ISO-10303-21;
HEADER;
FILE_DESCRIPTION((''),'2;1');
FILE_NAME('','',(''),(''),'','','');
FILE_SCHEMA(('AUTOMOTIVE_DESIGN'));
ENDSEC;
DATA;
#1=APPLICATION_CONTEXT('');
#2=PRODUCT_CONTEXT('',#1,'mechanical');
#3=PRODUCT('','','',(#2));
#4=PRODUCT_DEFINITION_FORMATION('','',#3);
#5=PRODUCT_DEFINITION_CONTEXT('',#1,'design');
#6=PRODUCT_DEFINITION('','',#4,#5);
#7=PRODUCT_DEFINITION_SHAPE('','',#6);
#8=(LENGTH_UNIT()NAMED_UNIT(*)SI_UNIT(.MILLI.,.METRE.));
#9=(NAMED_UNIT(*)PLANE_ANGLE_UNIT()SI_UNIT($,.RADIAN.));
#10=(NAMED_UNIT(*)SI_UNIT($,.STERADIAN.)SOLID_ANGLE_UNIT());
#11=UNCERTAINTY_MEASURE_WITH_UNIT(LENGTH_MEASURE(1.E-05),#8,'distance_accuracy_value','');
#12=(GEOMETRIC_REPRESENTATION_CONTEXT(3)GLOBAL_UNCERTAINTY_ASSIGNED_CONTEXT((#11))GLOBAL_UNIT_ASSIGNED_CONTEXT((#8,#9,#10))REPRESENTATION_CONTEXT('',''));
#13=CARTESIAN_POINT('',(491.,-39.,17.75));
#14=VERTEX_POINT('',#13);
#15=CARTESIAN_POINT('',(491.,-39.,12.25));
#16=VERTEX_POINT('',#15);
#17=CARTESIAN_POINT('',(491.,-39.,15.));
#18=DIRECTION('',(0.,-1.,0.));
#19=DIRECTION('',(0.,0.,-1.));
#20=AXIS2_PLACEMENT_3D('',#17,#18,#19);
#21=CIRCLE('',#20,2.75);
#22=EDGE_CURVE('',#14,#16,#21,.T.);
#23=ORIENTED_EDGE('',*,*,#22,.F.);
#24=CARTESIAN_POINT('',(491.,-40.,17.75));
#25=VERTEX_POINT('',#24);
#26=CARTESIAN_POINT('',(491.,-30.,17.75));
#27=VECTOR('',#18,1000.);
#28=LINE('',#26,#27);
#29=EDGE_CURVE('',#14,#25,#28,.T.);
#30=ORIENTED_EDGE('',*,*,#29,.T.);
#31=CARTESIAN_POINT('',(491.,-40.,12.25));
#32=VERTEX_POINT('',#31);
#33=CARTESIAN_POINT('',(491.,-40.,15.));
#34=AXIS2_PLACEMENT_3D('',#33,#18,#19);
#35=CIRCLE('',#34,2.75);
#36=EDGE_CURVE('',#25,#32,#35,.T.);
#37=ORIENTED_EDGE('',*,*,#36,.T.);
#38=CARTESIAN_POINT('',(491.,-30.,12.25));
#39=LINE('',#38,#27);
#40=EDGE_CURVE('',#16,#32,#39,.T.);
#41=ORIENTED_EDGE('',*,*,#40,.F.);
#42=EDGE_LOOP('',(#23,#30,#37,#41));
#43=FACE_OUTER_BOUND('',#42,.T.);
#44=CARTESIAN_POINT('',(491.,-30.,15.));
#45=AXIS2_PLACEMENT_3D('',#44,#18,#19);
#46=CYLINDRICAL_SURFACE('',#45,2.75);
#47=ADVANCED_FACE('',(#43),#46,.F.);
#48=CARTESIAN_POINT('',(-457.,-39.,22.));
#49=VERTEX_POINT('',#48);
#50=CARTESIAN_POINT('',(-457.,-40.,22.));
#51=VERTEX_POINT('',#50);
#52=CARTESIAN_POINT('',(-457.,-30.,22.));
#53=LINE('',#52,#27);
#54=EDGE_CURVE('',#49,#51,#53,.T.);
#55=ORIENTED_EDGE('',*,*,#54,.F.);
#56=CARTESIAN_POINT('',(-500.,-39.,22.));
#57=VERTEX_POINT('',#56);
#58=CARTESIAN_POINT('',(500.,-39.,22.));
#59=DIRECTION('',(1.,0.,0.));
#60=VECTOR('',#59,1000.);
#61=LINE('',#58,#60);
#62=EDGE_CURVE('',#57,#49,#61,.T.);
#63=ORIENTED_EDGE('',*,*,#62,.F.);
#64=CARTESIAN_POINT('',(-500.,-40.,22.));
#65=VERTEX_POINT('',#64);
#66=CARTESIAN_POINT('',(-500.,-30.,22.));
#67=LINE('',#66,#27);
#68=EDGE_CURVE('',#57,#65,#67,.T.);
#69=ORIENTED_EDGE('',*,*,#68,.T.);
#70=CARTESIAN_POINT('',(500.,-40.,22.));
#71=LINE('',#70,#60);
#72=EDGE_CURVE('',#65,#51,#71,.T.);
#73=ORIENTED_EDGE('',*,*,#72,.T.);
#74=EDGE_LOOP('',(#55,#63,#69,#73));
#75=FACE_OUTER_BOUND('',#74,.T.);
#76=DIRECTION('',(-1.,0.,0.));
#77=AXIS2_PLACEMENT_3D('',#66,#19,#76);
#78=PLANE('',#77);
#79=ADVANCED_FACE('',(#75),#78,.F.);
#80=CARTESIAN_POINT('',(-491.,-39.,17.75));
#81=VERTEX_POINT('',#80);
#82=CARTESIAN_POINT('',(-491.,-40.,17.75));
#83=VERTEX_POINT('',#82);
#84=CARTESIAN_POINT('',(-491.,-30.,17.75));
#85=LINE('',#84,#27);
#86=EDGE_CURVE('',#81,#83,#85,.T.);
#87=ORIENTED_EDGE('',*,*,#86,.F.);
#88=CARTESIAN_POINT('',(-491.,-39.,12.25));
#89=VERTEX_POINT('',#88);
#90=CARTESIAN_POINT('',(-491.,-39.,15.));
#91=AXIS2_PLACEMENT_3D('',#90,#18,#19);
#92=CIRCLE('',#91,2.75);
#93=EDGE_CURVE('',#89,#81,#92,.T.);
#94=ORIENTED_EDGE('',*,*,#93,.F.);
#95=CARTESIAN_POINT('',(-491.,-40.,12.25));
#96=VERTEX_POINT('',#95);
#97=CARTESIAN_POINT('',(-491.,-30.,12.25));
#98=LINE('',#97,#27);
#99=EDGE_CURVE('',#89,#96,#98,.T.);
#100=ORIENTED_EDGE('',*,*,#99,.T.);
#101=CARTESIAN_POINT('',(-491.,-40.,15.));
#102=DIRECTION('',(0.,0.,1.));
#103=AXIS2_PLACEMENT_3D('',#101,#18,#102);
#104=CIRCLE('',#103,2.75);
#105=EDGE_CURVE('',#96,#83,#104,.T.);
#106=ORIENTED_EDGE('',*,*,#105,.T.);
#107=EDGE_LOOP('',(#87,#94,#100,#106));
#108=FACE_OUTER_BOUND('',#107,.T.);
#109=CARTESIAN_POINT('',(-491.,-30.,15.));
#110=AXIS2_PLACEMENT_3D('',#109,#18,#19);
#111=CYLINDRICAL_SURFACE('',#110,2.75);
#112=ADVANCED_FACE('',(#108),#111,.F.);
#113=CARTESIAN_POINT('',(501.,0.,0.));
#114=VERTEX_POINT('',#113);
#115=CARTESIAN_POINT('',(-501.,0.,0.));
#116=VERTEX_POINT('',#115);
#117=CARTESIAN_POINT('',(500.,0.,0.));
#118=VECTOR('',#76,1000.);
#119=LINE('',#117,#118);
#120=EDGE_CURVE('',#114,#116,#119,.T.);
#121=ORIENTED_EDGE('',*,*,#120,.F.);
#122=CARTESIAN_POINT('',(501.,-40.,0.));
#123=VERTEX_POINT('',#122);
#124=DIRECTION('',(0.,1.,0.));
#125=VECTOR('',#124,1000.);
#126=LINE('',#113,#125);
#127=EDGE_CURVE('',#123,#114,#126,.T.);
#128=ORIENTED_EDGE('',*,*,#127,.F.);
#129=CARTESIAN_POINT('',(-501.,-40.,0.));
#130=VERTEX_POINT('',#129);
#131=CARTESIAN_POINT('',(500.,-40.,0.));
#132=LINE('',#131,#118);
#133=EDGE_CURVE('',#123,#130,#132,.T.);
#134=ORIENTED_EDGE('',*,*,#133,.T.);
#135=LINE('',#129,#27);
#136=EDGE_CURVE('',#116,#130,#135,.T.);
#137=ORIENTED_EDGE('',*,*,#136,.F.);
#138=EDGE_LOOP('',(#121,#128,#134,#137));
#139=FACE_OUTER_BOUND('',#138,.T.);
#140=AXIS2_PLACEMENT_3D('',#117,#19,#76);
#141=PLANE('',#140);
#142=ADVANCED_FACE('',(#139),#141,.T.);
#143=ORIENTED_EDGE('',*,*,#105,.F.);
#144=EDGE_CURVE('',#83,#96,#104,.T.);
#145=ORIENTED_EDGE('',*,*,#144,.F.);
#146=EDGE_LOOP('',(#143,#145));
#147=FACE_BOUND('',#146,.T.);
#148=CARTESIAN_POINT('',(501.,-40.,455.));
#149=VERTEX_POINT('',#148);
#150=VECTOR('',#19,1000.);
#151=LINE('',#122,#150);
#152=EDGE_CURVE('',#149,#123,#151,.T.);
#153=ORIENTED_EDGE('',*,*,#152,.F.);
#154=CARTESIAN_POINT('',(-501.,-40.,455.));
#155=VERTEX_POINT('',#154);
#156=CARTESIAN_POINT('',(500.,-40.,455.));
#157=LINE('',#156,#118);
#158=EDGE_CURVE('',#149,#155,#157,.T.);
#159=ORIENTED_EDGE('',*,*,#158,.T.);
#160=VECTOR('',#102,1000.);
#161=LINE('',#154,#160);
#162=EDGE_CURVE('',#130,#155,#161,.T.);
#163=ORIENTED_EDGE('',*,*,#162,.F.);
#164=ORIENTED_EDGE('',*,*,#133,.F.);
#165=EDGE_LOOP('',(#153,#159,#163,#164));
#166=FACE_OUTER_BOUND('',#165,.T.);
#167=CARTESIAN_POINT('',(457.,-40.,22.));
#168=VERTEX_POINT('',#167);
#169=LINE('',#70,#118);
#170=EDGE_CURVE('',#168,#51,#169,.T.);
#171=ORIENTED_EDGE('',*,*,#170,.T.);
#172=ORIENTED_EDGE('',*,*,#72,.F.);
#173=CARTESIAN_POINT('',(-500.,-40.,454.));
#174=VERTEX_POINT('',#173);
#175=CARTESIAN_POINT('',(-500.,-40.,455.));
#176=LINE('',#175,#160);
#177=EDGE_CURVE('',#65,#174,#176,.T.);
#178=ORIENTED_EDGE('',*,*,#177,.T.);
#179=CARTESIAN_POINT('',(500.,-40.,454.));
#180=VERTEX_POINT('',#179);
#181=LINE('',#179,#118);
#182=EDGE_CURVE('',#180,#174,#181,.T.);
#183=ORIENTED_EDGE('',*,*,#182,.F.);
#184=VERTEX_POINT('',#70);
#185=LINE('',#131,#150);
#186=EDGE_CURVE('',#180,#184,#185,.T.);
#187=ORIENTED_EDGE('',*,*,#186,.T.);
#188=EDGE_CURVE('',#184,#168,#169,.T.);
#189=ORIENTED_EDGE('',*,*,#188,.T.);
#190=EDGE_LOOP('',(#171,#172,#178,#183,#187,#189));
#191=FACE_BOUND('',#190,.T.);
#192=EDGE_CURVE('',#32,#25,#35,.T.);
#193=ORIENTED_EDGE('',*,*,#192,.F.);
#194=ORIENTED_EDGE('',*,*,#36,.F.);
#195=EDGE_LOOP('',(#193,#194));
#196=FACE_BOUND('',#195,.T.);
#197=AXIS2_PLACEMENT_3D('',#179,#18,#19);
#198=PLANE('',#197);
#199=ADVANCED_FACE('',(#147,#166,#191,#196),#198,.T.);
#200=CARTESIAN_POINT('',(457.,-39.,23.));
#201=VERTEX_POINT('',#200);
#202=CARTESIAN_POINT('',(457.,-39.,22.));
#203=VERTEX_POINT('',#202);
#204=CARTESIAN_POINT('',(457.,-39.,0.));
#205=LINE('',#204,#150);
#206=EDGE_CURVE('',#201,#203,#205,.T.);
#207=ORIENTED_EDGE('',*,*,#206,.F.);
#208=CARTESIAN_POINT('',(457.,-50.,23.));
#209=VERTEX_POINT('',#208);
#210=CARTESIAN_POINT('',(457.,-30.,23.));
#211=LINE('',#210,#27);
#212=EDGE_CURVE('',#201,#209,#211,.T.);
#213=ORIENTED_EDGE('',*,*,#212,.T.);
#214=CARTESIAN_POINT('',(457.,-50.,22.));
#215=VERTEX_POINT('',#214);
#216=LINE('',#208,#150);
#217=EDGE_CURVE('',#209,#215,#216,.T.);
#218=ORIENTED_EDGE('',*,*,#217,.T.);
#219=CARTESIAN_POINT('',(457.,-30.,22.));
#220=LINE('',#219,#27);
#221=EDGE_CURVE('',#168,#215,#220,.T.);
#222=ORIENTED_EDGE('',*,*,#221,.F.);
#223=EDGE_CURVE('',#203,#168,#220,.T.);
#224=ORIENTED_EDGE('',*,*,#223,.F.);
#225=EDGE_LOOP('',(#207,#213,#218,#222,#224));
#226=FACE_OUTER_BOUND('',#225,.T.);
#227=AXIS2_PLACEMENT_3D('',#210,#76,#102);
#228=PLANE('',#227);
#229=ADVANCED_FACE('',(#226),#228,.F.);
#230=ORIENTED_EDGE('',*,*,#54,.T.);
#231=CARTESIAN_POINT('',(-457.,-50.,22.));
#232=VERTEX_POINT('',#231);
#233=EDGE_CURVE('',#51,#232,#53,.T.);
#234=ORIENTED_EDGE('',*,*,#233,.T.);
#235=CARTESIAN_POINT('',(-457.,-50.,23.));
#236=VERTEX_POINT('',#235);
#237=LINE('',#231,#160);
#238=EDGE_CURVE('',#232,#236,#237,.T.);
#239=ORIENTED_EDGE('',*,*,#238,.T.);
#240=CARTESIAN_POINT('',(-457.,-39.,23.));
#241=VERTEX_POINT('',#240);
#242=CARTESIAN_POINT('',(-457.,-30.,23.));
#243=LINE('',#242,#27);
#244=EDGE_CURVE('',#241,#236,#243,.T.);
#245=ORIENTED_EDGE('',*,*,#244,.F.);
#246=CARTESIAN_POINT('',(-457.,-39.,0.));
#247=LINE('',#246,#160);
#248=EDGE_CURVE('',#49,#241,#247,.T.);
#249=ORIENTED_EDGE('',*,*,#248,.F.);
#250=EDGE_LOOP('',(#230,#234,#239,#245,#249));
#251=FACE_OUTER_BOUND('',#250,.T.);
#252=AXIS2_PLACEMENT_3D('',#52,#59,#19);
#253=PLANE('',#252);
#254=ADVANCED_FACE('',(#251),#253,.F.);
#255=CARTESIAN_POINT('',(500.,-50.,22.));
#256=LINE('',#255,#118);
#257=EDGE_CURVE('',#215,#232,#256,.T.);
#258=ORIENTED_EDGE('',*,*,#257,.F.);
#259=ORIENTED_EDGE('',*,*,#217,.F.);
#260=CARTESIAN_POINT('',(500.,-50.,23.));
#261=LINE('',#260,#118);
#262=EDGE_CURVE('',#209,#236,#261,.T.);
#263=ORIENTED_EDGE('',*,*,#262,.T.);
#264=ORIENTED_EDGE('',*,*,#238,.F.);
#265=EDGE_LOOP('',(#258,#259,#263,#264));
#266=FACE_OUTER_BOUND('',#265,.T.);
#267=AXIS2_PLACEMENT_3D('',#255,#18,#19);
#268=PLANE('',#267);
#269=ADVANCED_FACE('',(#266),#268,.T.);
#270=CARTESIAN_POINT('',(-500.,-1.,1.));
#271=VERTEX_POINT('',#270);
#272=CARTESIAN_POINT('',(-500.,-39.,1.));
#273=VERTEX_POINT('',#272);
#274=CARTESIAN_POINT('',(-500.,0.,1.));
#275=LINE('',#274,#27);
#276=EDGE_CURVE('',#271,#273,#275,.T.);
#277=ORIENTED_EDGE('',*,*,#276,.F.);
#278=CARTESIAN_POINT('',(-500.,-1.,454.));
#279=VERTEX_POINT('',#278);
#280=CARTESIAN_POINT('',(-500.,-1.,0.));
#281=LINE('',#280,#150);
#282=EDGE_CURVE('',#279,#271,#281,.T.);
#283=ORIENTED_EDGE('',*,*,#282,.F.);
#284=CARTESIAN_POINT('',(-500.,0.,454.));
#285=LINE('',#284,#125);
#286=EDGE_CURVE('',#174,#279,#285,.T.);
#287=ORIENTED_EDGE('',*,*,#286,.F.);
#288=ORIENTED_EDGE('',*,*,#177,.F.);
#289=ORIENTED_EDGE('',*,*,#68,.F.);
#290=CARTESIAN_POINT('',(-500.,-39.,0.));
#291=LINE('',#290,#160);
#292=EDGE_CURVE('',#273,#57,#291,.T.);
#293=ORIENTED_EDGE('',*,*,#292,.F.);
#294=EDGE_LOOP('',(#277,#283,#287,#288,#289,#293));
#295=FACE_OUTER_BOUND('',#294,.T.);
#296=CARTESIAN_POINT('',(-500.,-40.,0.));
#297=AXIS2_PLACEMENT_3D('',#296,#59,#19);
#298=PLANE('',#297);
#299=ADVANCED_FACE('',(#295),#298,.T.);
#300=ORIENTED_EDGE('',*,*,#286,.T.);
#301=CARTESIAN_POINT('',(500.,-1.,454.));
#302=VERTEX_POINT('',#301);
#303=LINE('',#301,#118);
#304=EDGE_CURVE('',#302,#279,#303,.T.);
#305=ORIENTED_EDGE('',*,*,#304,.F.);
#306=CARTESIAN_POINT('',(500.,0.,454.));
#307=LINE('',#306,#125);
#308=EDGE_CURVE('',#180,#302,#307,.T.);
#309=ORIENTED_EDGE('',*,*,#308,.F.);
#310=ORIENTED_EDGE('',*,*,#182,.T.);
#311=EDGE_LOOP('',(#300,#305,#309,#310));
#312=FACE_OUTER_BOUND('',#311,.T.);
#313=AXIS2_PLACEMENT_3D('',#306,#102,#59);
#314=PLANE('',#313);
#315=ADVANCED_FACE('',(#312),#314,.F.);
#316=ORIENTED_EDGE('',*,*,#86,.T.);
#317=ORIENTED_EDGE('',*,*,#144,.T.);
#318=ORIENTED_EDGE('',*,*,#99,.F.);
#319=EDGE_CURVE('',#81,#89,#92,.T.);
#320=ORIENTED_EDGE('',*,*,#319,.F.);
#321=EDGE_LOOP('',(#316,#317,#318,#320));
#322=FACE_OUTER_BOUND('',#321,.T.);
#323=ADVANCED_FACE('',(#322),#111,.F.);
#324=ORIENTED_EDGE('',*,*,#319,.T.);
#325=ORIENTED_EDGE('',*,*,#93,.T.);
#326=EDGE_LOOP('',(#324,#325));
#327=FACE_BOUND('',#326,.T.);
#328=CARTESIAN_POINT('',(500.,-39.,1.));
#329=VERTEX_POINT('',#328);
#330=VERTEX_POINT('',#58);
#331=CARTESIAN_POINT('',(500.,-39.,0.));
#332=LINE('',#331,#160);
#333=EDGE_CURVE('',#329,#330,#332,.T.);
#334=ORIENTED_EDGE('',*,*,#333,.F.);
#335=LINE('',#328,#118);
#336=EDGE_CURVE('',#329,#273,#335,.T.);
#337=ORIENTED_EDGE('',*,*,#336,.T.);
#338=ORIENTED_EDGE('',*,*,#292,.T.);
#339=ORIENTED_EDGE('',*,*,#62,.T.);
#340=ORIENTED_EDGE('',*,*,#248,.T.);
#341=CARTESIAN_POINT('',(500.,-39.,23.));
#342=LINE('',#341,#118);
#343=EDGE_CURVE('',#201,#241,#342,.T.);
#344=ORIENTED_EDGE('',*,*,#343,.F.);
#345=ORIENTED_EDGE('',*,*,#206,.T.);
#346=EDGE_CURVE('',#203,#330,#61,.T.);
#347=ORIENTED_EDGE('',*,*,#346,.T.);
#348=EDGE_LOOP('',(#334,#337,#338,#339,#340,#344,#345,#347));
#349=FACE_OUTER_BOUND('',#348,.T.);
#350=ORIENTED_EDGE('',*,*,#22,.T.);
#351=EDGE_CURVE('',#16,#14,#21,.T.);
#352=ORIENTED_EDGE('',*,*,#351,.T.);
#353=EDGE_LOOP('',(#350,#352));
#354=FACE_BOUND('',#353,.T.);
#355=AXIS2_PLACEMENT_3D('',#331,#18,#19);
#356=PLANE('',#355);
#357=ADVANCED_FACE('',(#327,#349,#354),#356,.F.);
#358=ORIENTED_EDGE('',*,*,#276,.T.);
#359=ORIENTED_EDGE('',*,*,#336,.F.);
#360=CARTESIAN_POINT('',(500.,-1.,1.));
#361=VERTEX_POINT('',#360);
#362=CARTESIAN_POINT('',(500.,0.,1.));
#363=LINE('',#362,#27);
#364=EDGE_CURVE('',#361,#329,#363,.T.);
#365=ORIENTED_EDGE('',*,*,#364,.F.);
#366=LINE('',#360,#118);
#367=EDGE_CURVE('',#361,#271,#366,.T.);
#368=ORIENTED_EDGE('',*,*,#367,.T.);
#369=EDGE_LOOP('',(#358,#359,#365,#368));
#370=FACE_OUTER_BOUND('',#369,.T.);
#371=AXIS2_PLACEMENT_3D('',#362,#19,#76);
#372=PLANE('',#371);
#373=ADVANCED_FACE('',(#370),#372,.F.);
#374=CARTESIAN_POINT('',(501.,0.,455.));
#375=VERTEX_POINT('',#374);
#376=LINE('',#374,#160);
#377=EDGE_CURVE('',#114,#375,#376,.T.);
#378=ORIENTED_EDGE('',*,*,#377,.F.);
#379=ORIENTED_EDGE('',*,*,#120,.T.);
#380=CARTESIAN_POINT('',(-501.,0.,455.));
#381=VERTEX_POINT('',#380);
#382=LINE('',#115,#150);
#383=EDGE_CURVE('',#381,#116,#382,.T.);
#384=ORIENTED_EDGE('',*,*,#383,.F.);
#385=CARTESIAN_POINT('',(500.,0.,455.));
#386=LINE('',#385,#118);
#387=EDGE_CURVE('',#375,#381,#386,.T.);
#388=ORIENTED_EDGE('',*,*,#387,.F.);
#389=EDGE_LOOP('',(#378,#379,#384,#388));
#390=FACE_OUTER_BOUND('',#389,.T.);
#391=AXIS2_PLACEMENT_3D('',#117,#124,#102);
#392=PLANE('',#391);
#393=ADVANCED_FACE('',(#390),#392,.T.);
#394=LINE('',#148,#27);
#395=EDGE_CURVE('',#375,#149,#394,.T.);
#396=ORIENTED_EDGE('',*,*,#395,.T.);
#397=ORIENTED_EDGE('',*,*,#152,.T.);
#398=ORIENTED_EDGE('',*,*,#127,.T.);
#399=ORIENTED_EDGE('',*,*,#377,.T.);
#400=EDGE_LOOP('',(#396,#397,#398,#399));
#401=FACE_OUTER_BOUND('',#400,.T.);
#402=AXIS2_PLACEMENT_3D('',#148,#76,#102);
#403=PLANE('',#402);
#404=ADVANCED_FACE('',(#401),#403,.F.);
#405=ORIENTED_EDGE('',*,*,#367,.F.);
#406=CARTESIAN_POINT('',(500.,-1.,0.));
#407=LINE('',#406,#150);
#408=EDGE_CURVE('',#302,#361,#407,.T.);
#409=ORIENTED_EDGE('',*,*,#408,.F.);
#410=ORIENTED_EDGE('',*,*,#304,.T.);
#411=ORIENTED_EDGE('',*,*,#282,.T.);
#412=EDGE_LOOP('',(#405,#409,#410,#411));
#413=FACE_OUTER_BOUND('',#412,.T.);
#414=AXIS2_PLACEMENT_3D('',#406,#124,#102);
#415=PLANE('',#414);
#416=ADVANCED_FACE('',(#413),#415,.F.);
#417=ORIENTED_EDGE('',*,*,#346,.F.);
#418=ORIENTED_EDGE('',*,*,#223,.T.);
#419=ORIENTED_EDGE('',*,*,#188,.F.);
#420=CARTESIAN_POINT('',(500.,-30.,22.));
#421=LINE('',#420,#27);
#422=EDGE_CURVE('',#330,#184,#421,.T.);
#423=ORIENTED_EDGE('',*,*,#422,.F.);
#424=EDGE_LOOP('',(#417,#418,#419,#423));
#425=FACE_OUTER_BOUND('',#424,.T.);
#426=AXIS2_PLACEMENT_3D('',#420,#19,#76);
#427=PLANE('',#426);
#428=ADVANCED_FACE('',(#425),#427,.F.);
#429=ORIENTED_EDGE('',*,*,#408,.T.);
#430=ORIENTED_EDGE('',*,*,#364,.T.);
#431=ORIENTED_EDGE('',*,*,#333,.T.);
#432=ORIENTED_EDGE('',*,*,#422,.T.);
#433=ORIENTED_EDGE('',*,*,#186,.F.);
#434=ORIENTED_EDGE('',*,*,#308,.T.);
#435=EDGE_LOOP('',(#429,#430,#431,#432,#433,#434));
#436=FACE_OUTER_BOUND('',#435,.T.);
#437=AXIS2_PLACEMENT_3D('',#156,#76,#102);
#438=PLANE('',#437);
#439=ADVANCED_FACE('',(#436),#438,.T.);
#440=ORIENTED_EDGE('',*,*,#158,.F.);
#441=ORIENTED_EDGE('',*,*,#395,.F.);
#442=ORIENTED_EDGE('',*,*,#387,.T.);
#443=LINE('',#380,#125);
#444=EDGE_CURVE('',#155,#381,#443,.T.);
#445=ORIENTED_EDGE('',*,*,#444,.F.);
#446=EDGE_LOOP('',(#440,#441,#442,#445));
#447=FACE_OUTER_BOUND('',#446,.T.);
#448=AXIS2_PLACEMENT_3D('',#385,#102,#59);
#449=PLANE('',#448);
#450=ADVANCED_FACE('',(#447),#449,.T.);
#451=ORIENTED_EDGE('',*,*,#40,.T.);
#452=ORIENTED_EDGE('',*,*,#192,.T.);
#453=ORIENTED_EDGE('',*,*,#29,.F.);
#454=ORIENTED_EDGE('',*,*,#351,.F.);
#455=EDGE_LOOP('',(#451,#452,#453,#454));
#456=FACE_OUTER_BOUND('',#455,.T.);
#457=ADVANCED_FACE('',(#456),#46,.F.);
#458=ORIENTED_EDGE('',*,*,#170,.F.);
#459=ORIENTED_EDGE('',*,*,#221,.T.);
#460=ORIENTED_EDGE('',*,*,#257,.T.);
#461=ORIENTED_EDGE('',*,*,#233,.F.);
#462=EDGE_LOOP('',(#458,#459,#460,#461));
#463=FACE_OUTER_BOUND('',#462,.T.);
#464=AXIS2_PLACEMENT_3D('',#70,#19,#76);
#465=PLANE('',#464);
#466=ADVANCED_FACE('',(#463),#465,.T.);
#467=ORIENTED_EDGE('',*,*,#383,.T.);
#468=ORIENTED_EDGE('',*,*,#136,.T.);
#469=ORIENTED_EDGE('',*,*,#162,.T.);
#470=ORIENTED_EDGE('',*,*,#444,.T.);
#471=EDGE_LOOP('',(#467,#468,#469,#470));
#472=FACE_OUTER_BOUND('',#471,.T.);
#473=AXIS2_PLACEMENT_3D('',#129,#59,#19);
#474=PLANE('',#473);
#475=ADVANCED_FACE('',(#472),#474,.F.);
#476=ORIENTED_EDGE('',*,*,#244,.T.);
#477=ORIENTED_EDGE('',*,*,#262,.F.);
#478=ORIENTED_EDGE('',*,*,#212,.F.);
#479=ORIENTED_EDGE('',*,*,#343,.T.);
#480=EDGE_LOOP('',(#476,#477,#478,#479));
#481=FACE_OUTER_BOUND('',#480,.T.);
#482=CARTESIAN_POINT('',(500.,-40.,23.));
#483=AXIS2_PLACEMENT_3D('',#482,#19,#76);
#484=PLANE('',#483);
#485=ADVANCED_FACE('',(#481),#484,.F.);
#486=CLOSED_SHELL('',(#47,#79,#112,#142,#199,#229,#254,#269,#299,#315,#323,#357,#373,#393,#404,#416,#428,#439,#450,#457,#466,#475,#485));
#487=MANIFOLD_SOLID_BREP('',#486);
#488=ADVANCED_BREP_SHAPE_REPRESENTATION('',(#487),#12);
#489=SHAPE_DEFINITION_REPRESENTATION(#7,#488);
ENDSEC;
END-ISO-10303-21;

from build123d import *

# Parameters (mm, degrees)
EXTRUDE_THIN1_DEPTH = 500
SKETCH3_W           = 455
SKETCH3_H           = 40
EXTRUDE1_DEPTH      = 1
SKETCH7_W           = 455
SKETCH7_H           = 40
EXTRUDE3_DEPTH      = 1
SKETCH8_W           = 43
SKETCH8_H           = 1
CUT_EXTRUDE1_DEPTH  = 20
SKETCH9_R           = 2.75
CUT_EXTRUDE2_DEPTH  = 10


with BuildPart() as part:
    # Sketch2 → Extrude-Thin1 (new, symmetric)
    with BuildSketch(Plane(origin=(0, 0, 0), x_dir=(0, 0, -1), z_dir=(1, 0, 0))):
        Polygon((-22, -50), (-22, -40), (0, -40), (0, 0), (-455, 0), (-455, -40), (-454, -40), (-454, -1), (-1, -1), (-1, -39), (-23, -39), (-23, -50), align=None)
    extrude(amount=EXTRUDE_THIN1_DEPTH, both=True)

    # Sketch3 → Extrude1 (add)
    with BuildSketch(Plane(origin=(500, 0, 0), x_dir=(0, 0, -1), z_dir=(1, 0, 0))):
        with Locations((-227.5, -20)):
            Rectangle(SKETCH3_W, SKETCH3_H)
    extrude(amount=EXTRUDE1_DEPTH)

    # Sketch7 → Extrude3 (add)
    with BuildSketch(Plane.ZY.offset(500)):
        with Locations((227.5, -20)):
            Rectangle(SKETCH7_W, SKETCH7_H)
    extrude(amount=EXTRUDE3_DEPTH)

    # Sketch8 → Cut-Extrude1 (cut)
    with BuildSketch(Plane.XZ.offset(50)):
        with Locations((478.5, 22.5)):
            Rectangle(SKETCH8_W, SKETCH8_H)
        with Locations((-478.5, 22.5)):
            Rectangle(SKETCH8_W, SKETCH8_H)
    extrude(amount=-CUT_EXTRUDE1_DEPTH, mode=Mode.SUBTRACT)

    # Sketch9 → Cut-Extrude2 (cut)
    with BuildSketch(Plane.XZ.offset(40)):
        with Locations(Location((491, 15, 0), (0, 0, 270))):
            Circle(SKETCH9_R)
        with Locations(Location((-491, 15, 0), (0, 0, 270))):
            Circle(SKETCH9_R)
    extrude(amount=-CUT_EXTRUDE2_DEPTH, mode=Mode.SUBTRACT)


solid = part.part
